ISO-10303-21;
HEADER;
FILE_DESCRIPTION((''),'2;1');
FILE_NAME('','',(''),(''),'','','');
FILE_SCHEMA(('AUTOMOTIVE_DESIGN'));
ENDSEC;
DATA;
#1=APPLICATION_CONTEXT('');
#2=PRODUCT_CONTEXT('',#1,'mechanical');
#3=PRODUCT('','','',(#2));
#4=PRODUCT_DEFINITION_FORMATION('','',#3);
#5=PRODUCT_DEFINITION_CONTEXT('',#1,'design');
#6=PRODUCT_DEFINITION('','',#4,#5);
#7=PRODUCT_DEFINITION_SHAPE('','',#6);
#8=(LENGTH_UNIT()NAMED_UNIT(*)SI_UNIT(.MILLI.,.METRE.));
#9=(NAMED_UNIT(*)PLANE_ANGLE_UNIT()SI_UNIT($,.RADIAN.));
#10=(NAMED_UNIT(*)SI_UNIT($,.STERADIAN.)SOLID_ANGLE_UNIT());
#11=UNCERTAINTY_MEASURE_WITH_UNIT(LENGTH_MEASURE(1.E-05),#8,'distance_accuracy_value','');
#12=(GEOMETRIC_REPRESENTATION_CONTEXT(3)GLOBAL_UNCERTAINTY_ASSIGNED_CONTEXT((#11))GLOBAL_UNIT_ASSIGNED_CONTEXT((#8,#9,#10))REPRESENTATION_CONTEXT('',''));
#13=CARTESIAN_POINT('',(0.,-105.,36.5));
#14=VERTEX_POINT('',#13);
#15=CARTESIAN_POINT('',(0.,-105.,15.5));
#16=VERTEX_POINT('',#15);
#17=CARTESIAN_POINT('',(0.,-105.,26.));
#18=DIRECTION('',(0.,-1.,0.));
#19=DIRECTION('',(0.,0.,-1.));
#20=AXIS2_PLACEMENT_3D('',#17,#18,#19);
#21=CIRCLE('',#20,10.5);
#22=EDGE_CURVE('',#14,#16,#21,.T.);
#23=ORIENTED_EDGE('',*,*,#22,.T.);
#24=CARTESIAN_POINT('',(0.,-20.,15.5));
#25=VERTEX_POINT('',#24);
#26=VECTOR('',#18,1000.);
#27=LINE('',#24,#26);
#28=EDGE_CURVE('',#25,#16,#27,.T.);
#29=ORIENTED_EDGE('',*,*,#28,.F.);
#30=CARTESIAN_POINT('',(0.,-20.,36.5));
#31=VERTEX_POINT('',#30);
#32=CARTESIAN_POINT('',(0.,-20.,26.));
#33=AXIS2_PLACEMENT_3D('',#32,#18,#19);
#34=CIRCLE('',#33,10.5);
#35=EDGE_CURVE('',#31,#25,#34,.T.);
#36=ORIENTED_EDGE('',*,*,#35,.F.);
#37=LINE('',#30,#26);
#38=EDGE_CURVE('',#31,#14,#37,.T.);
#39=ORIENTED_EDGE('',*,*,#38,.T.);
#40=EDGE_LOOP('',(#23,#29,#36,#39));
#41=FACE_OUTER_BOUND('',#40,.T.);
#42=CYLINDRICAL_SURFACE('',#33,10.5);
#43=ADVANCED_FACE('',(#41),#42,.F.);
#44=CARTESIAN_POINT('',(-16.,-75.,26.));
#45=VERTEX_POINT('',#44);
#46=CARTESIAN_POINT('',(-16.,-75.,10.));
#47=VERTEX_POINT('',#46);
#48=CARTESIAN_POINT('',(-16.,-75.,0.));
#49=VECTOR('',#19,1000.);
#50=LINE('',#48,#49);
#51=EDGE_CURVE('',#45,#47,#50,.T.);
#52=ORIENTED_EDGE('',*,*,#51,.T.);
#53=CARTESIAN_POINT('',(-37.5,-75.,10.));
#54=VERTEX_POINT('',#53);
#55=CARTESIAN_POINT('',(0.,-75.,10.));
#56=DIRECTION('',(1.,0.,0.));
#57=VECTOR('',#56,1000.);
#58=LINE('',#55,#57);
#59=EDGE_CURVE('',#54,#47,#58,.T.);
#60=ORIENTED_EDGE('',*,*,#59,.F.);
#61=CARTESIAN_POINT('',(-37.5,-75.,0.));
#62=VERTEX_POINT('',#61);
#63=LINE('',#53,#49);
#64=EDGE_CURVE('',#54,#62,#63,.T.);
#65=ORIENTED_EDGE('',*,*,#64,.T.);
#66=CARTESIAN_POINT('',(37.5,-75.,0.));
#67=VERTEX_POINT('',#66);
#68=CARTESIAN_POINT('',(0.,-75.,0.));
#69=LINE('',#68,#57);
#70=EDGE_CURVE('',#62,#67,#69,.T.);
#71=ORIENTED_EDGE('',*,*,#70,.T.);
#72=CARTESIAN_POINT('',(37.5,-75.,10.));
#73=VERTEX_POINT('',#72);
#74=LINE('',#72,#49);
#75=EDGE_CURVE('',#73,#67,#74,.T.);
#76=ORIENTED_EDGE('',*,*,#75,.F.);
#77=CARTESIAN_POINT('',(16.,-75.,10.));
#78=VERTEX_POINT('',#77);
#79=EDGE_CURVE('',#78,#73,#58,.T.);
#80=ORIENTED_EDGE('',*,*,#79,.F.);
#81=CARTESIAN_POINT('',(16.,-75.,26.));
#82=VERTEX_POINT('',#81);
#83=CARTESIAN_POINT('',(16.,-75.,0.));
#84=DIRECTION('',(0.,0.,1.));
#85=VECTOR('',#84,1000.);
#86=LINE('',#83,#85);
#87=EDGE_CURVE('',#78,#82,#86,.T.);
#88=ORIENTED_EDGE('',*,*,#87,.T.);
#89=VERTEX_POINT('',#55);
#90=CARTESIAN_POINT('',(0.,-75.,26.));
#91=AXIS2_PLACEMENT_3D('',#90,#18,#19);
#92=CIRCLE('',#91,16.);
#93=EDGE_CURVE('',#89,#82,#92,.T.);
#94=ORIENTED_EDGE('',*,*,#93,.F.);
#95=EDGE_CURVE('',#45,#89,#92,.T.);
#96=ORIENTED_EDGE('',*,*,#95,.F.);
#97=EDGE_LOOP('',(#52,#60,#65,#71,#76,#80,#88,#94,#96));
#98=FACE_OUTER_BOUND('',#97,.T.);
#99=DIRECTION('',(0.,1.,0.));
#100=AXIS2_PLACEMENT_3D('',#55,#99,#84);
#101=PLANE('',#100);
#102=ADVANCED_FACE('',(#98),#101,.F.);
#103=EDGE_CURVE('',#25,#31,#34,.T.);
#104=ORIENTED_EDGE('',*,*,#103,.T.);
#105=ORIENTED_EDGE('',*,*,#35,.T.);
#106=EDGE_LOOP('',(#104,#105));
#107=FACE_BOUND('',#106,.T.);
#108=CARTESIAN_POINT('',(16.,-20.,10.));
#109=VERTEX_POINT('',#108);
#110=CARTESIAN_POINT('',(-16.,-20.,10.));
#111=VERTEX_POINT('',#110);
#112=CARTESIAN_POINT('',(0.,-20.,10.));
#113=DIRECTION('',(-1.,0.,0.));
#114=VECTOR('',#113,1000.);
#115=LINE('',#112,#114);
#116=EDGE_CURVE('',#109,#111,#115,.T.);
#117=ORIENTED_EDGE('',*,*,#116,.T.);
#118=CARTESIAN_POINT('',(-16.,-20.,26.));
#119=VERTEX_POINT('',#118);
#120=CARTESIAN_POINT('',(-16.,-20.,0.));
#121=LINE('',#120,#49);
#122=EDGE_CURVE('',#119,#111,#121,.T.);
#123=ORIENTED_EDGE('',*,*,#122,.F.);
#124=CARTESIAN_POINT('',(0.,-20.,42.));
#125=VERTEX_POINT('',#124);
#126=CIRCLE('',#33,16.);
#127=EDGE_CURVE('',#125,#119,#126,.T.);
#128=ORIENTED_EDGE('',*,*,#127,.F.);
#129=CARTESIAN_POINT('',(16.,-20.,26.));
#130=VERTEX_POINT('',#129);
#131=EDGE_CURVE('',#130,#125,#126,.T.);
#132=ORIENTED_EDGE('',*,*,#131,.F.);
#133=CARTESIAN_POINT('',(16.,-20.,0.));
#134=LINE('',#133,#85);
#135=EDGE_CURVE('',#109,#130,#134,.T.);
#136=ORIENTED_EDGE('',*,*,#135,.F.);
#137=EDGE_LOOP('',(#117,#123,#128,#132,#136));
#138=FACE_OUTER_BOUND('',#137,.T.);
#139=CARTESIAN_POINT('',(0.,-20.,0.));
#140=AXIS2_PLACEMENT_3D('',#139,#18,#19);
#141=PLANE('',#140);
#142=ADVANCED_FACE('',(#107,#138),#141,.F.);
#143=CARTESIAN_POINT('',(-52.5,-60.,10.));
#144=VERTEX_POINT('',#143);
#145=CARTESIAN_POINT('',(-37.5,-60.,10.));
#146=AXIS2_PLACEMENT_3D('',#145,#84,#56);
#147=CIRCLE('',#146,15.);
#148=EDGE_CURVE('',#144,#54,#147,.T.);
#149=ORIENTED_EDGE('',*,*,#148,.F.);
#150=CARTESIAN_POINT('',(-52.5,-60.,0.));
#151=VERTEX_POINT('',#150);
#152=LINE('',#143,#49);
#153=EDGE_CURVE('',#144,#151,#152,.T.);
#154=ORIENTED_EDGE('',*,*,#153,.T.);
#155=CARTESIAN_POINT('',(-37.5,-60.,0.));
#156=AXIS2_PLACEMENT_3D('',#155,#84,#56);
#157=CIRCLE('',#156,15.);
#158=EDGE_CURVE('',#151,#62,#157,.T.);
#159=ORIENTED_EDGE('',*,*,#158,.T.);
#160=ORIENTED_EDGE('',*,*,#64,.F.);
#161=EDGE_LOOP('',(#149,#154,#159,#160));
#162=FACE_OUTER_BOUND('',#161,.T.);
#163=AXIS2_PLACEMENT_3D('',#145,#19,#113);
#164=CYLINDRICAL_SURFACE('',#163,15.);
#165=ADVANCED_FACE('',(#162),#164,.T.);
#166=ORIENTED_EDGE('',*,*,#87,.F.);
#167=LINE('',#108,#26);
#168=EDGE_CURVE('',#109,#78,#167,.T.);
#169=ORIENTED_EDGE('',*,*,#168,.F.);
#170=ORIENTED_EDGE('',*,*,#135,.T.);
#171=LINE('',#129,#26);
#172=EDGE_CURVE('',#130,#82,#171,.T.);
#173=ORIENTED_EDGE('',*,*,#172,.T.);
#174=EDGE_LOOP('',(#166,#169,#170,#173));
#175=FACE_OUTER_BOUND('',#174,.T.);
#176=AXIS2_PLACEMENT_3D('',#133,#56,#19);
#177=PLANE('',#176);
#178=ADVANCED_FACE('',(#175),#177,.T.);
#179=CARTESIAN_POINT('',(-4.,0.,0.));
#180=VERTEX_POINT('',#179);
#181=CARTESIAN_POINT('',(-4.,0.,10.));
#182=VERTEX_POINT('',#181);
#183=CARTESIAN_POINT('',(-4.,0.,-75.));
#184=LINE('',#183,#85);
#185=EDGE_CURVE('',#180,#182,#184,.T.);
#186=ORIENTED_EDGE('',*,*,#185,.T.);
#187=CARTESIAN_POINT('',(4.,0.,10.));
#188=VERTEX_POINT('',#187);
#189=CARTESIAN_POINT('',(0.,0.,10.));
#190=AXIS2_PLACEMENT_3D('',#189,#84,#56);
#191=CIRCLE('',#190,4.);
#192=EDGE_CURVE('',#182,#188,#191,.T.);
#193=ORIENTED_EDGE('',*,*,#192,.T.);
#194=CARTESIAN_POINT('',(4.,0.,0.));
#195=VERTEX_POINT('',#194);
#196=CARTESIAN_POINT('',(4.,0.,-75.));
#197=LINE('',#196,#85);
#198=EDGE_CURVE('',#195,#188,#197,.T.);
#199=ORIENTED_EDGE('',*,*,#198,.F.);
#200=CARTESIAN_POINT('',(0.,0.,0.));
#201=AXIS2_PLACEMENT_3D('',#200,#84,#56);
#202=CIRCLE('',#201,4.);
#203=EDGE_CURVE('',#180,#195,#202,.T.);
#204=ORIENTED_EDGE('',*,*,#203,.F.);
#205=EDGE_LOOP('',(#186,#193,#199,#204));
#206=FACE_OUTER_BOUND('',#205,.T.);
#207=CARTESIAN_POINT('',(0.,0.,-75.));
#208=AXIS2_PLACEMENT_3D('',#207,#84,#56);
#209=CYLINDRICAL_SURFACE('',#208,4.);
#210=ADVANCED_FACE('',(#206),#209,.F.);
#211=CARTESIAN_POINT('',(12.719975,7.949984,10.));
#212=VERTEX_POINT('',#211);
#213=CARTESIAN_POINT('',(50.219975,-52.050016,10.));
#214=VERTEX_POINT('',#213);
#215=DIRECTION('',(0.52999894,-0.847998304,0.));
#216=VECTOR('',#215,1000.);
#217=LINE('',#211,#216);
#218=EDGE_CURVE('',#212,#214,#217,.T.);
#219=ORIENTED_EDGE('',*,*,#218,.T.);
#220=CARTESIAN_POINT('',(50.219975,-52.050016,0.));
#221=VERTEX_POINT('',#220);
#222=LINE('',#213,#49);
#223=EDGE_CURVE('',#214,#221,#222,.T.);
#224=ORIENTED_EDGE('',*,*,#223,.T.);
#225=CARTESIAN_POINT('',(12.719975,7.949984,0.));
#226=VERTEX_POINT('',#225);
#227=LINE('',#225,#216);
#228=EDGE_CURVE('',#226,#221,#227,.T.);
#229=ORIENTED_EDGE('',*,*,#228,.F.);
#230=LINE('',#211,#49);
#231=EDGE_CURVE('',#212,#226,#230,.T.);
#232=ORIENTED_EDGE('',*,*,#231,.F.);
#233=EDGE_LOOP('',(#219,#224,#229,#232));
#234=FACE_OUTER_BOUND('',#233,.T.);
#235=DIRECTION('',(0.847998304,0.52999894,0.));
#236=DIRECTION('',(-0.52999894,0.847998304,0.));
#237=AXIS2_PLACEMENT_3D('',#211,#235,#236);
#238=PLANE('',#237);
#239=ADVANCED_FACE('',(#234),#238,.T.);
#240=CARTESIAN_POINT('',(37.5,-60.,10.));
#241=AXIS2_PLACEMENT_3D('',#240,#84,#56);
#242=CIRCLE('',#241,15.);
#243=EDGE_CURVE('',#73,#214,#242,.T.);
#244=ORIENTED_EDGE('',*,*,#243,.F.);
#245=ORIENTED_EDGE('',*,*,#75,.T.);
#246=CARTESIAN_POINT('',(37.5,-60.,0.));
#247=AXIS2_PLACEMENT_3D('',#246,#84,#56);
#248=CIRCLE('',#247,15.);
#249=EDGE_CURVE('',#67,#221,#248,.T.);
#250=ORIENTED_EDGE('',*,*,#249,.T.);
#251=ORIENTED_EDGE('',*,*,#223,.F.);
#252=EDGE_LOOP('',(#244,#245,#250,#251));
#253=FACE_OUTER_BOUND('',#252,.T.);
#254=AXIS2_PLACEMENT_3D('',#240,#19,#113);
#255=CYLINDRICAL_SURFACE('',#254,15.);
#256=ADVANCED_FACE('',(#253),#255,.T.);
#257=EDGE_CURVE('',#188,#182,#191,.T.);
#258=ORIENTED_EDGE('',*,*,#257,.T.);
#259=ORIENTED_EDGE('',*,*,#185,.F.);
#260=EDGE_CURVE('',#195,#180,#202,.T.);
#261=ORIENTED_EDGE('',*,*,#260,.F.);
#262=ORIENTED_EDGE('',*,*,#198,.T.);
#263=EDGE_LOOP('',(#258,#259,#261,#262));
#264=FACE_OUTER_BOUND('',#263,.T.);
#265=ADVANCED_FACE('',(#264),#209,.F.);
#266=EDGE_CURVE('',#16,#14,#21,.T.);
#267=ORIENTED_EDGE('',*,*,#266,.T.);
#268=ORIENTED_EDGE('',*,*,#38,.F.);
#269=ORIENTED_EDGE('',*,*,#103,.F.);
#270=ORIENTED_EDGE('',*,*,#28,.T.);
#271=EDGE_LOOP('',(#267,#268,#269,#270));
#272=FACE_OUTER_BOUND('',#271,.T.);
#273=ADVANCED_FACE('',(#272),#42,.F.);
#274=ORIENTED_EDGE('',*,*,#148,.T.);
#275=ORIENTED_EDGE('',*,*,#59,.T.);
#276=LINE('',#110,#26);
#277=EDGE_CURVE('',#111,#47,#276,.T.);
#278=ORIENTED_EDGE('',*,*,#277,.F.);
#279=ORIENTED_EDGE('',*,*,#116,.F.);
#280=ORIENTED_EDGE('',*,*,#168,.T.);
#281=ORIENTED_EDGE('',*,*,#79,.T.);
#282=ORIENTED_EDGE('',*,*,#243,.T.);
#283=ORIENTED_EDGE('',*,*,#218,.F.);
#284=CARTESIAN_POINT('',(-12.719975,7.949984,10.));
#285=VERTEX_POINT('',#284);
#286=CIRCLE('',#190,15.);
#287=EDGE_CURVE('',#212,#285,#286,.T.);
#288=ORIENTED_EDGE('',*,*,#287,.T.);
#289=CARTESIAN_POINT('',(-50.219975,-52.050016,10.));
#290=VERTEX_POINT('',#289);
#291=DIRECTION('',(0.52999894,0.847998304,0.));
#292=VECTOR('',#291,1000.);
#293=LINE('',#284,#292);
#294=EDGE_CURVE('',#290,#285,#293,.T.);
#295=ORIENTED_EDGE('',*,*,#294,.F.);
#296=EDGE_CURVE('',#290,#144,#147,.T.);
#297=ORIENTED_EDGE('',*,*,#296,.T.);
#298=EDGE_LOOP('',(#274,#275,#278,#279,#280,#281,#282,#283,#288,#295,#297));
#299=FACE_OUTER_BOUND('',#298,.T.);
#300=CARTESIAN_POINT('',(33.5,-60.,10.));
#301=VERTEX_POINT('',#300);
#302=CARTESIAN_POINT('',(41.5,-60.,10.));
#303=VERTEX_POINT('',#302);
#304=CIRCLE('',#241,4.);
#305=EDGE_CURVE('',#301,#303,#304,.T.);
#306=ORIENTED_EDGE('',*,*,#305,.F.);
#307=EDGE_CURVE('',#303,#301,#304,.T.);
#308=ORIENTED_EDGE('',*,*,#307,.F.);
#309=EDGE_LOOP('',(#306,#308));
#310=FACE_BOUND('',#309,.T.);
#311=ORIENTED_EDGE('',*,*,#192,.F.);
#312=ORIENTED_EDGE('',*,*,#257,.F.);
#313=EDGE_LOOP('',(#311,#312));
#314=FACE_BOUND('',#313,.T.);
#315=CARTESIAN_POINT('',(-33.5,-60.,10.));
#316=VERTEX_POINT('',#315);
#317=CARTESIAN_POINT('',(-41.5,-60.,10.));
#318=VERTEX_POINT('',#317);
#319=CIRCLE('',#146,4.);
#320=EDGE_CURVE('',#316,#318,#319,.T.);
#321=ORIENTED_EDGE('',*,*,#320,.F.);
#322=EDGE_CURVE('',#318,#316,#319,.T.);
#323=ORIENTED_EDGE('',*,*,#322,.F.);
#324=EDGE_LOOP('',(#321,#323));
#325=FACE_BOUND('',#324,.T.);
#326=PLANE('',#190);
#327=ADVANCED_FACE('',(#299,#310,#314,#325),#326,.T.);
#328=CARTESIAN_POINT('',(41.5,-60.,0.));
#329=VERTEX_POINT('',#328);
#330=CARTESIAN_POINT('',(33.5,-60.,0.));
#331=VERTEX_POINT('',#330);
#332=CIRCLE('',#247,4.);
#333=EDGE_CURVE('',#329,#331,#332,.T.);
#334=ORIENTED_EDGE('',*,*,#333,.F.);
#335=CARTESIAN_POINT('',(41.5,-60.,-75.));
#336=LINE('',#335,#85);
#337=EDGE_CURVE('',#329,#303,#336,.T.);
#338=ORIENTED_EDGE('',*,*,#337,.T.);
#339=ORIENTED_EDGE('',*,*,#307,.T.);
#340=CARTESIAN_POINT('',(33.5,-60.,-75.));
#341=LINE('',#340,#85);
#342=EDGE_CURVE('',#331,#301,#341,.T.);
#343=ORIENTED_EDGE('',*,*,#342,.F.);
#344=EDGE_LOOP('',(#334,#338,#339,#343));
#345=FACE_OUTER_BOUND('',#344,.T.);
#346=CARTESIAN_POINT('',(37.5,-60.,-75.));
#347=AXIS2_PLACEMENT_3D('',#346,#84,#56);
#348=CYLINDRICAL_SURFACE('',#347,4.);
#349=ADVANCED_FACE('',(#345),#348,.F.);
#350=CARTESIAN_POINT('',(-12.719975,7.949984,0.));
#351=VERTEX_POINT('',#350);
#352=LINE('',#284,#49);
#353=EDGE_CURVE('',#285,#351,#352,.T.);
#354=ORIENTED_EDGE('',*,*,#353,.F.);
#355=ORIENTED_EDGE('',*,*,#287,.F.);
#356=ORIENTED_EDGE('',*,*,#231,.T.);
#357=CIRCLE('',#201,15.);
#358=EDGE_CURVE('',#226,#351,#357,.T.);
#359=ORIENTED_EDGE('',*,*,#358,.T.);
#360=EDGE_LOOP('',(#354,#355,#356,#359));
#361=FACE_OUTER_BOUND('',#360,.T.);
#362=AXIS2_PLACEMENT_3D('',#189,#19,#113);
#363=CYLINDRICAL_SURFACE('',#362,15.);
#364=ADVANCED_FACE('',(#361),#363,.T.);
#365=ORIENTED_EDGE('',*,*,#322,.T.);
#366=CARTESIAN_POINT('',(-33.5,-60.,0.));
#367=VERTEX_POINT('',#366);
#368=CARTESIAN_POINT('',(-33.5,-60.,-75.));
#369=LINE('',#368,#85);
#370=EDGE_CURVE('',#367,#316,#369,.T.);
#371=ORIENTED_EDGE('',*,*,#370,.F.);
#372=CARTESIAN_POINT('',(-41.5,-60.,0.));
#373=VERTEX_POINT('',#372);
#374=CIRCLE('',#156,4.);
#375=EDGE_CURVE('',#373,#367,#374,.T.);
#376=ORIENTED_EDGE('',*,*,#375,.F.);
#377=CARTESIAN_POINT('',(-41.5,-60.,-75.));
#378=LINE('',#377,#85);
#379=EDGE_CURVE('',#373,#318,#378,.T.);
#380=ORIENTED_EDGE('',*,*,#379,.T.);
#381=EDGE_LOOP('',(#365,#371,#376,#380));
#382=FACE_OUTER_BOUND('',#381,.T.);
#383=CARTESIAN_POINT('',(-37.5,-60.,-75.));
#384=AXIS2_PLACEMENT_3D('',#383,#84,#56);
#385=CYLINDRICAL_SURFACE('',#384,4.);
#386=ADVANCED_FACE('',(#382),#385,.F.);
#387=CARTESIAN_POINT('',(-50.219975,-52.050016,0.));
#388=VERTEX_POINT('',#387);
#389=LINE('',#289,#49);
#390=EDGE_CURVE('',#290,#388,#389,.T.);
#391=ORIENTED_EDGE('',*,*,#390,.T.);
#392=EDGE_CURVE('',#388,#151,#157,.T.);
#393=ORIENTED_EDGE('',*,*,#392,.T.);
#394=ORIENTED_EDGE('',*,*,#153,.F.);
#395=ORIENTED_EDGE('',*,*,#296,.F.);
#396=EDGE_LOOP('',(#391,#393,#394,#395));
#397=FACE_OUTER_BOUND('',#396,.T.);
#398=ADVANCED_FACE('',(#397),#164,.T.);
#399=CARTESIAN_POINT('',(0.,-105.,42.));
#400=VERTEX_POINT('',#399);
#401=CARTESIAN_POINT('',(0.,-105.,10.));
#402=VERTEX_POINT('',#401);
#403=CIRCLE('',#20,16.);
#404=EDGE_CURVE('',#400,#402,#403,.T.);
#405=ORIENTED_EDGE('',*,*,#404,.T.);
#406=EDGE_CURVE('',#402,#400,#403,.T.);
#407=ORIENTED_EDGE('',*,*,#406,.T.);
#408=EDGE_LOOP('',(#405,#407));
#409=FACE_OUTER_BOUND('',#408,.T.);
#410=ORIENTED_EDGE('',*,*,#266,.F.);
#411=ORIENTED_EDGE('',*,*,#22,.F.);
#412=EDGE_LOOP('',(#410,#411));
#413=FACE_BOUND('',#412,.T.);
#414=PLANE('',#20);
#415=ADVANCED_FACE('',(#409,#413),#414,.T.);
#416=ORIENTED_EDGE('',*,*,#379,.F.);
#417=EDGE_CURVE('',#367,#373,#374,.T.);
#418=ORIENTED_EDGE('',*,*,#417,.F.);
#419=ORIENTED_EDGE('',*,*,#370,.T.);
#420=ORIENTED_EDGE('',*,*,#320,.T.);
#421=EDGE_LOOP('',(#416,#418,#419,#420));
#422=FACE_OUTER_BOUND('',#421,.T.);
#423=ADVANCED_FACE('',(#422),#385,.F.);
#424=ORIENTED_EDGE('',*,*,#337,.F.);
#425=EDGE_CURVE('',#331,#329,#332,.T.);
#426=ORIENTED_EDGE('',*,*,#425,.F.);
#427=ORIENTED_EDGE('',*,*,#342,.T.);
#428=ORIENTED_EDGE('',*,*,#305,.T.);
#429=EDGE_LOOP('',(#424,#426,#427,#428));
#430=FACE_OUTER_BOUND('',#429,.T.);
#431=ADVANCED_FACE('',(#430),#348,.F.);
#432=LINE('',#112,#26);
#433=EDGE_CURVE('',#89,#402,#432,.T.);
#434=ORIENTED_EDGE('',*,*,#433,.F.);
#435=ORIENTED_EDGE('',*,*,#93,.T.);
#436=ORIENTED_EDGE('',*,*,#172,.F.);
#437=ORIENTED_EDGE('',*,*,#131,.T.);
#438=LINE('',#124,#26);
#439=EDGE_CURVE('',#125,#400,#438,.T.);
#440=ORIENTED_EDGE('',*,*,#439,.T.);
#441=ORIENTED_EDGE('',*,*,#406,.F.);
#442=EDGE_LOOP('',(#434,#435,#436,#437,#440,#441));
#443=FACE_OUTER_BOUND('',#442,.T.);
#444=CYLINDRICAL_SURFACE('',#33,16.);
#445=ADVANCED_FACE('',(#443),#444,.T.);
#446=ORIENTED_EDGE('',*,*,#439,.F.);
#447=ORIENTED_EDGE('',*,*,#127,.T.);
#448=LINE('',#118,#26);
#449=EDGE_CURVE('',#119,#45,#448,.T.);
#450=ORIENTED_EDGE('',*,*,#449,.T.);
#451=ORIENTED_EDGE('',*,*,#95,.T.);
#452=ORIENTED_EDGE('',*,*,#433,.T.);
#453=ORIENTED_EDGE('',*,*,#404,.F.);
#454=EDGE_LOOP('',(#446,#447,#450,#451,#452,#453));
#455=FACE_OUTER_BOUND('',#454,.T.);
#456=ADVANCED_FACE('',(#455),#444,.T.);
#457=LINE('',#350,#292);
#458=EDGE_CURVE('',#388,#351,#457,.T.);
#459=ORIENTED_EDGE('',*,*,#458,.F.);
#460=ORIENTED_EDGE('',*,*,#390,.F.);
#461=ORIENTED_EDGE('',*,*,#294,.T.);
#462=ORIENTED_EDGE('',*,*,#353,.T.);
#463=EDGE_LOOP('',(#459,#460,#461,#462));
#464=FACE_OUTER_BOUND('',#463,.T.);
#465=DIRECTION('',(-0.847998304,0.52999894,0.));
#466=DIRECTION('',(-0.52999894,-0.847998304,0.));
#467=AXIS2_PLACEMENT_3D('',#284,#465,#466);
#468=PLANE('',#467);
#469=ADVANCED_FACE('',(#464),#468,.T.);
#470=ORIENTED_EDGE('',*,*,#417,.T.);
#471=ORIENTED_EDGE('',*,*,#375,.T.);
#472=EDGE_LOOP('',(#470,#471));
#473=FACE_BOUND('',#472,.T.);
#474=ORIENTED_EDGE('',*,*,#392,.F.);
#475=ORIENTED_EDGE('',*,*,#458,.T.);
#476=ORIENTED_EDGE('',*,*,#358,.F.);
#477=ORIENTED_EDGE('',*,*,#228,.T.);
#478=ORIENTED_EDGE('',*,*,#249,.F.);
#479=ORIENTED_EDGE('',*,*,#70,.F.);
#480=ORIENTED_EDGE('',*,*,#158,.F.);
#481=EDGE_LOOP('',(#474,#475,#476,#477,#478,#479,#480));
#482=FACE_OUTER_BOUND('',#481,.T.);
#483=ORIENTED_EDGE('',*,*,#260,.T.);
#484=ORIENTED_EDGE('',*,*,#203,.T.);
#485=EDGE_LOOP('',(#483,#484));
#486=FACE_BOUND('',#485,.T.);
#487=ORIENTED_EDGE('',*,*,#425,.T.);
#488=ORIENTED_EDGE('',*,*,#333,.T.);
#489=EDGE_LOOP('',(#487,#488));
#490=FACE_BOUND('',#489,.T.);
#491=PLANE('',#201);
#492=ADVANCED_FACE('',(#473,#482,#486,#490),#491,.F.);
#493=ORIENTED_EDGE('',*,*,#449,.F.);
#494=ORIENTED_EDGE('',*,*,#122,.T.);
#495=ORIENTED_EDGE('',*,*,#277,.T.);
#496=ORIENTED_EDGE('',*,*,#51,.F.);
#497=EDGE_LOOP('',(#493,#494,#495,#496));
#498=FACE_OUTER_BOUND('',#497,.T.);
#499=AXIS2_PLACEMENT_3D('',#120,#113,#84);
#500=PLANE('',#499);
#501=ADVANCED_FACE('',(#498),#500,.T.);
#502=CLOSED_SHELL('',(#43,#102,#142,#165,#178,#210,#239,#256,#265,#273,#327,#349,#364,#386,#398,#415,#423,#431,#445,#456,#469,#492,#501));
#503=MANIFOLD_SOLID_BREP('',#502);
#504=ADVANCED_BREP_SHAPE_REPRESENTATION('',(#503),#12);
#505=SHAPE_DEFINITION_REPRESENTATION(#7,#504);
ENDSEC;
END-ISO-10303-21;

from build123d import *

# Parameters (mm, degrees)
TRIANGULAR_BASE_PLATE_DEPTH   = 10
TUBE_SUPPORT_BLOCK_PROFILE_W  = 16
TUBE_SUPPORT_BLOCK_PROFILE_H  = 10
TUBE_SUPPORT_BLOCK_DEPTH      = 55
SUPPORT_WEB_PROFILE_W         = 16
SUPPORT_WEB_PROFILE_H         = 6
SUPPORT_WEB_DEPTH             = 55
TUBE_PROFILE_32_R             = 16
ROUND_TUBE_32_DEPTH           = 55
TUBE_START                    = 30
TUBE_EXTENSION_PROFILE_32_R   = 16
TUBE_EXTENSION_32_DEPTH       = 30
TUBE_BORE_PROFILE_21_R        = 10.5
TUBE_BORE_21_DEPTH            = 85
MOUNTING_HOLES_PROFILE_3X_8_R = 4
MOUNTING_HOLES_3X_8_DEPTH     = 85


with BuildPart() as part:
    # Base Plate Profile → Triangular Base Plate (new body)
    with BuildSketch(Plane.XY):
        with BuildLine():
            Line((-50.21997456, -52.0500159), (-12.71997456, 7.9499841))
            ThreePointArc((-12.71997456, 7.9499841), (0, 15), (12.71997456, 7.9499841))
            Line((12.71997456, 7.9499841), (50.21997456, -52.0500159))
            ThreePointArc((50.21997456, -52.0500159), (50.619637219, -67.271527986), (37.5, -75))
            Line((37.5, -75), (-37.5, -75))
            ThreePointArc((-37.5, -75), (-50.619637219, -67.271527986), (-50.21997456, -52.0500159))
        make_face()
    extrude(amount=TRIANGULAR_BASE_PLATE_DEPTH)

    # Tube Support Block Profile → Tube Support Block (add)
    with BuildSketch(Plane.XZ.offset(75)):
        with Locations((-8, 15)):
            Rectangle(TUBE_SUPPORT_BLOCK_PROFILE_W, TUBE_SUPPORT_BLOCK_PROFILE_H)
        with Locations((8, 15)):
            Rectangle(TUBE_SUPPORT_BLOCK_PROFILE_W, TUBE_SUPPORT_BLOCK_PROFILE_H)
    extrude(amount=-TUBE_SUPPORT_BLOCK_DEPTH)

    # Support Web Profile → Support Web (add)
    with BuildSketch(Plane.XZ.offset(75)):
        with Locations((-8, 23)):
            Rectangle(SUPPORT_WEB_PROFILE_W, SUPPORT_WEB_PROFILE_H)
        with Locations((8, 23)):
            Rectangle(SUPPORT_WEB_PROFILE_W, SUPPORT_WEB_PROFILE_H)
    extrude(amount=-SUPPORT_WEB_DEPTH)

    # Tube Profile Ø32 → Round Tube Ø32 (add)
    with BuildSketch(Plane.XZ.offset(75)):
        with Locations((0, 26)):
            Circle(TUBE_PROFILE_32_R)
    extrude(amount=-ROUND_TUBE_32_DEPTH)

    # Tube Extension Profile Ø32 → Tube Extension Ø32 (add)
    with BuildSketch(Plane.XZ.offset(75).offset(TUBE_START)):
        with Locations(Location((0, 26, 0), (0, 0, 270))):
            Circle(TUBE_EXTENSION_PROFILE_32_R)
    extrude(amount=-TUBE_EXTENSION_32_DEPTH)

    # Tube Bore Profile Ø21 → Tube Bore Ø21 (cut)
    with BuildSketch(Plane.XZ.offset(105)):
        with Locations(Location((0, 26, 0), (0, 0, 270))):
            Circle(TUBE_BORE_PROFILE_21_R)
    extrude(amount=-TUBE_BORE_21_DEPTH, mode=Mode.SUBTRACT)

    # Mounting Holes Profile 3xØ8 → Mounting Holes 3xØ8 (cut)
    with BuildSketch(Plane.XY.offset(10)):
        Circle(MOUNTING_HOLES_PROFILE_3X_8_R)
        with Locations((-37.5, -60)):
            Circle(MOUNTING_HOLES_PROFILE_3X_8_R)
        with Locations((37.5, -60)):
            Circle(MOUNTING_HOLES_PROFILE_3X_8_R)
    extrude(amount=-MOUNTING_HOLES_3X_8_DEPTH, mode=Mode.SUBTRACT)


solid = part.part
